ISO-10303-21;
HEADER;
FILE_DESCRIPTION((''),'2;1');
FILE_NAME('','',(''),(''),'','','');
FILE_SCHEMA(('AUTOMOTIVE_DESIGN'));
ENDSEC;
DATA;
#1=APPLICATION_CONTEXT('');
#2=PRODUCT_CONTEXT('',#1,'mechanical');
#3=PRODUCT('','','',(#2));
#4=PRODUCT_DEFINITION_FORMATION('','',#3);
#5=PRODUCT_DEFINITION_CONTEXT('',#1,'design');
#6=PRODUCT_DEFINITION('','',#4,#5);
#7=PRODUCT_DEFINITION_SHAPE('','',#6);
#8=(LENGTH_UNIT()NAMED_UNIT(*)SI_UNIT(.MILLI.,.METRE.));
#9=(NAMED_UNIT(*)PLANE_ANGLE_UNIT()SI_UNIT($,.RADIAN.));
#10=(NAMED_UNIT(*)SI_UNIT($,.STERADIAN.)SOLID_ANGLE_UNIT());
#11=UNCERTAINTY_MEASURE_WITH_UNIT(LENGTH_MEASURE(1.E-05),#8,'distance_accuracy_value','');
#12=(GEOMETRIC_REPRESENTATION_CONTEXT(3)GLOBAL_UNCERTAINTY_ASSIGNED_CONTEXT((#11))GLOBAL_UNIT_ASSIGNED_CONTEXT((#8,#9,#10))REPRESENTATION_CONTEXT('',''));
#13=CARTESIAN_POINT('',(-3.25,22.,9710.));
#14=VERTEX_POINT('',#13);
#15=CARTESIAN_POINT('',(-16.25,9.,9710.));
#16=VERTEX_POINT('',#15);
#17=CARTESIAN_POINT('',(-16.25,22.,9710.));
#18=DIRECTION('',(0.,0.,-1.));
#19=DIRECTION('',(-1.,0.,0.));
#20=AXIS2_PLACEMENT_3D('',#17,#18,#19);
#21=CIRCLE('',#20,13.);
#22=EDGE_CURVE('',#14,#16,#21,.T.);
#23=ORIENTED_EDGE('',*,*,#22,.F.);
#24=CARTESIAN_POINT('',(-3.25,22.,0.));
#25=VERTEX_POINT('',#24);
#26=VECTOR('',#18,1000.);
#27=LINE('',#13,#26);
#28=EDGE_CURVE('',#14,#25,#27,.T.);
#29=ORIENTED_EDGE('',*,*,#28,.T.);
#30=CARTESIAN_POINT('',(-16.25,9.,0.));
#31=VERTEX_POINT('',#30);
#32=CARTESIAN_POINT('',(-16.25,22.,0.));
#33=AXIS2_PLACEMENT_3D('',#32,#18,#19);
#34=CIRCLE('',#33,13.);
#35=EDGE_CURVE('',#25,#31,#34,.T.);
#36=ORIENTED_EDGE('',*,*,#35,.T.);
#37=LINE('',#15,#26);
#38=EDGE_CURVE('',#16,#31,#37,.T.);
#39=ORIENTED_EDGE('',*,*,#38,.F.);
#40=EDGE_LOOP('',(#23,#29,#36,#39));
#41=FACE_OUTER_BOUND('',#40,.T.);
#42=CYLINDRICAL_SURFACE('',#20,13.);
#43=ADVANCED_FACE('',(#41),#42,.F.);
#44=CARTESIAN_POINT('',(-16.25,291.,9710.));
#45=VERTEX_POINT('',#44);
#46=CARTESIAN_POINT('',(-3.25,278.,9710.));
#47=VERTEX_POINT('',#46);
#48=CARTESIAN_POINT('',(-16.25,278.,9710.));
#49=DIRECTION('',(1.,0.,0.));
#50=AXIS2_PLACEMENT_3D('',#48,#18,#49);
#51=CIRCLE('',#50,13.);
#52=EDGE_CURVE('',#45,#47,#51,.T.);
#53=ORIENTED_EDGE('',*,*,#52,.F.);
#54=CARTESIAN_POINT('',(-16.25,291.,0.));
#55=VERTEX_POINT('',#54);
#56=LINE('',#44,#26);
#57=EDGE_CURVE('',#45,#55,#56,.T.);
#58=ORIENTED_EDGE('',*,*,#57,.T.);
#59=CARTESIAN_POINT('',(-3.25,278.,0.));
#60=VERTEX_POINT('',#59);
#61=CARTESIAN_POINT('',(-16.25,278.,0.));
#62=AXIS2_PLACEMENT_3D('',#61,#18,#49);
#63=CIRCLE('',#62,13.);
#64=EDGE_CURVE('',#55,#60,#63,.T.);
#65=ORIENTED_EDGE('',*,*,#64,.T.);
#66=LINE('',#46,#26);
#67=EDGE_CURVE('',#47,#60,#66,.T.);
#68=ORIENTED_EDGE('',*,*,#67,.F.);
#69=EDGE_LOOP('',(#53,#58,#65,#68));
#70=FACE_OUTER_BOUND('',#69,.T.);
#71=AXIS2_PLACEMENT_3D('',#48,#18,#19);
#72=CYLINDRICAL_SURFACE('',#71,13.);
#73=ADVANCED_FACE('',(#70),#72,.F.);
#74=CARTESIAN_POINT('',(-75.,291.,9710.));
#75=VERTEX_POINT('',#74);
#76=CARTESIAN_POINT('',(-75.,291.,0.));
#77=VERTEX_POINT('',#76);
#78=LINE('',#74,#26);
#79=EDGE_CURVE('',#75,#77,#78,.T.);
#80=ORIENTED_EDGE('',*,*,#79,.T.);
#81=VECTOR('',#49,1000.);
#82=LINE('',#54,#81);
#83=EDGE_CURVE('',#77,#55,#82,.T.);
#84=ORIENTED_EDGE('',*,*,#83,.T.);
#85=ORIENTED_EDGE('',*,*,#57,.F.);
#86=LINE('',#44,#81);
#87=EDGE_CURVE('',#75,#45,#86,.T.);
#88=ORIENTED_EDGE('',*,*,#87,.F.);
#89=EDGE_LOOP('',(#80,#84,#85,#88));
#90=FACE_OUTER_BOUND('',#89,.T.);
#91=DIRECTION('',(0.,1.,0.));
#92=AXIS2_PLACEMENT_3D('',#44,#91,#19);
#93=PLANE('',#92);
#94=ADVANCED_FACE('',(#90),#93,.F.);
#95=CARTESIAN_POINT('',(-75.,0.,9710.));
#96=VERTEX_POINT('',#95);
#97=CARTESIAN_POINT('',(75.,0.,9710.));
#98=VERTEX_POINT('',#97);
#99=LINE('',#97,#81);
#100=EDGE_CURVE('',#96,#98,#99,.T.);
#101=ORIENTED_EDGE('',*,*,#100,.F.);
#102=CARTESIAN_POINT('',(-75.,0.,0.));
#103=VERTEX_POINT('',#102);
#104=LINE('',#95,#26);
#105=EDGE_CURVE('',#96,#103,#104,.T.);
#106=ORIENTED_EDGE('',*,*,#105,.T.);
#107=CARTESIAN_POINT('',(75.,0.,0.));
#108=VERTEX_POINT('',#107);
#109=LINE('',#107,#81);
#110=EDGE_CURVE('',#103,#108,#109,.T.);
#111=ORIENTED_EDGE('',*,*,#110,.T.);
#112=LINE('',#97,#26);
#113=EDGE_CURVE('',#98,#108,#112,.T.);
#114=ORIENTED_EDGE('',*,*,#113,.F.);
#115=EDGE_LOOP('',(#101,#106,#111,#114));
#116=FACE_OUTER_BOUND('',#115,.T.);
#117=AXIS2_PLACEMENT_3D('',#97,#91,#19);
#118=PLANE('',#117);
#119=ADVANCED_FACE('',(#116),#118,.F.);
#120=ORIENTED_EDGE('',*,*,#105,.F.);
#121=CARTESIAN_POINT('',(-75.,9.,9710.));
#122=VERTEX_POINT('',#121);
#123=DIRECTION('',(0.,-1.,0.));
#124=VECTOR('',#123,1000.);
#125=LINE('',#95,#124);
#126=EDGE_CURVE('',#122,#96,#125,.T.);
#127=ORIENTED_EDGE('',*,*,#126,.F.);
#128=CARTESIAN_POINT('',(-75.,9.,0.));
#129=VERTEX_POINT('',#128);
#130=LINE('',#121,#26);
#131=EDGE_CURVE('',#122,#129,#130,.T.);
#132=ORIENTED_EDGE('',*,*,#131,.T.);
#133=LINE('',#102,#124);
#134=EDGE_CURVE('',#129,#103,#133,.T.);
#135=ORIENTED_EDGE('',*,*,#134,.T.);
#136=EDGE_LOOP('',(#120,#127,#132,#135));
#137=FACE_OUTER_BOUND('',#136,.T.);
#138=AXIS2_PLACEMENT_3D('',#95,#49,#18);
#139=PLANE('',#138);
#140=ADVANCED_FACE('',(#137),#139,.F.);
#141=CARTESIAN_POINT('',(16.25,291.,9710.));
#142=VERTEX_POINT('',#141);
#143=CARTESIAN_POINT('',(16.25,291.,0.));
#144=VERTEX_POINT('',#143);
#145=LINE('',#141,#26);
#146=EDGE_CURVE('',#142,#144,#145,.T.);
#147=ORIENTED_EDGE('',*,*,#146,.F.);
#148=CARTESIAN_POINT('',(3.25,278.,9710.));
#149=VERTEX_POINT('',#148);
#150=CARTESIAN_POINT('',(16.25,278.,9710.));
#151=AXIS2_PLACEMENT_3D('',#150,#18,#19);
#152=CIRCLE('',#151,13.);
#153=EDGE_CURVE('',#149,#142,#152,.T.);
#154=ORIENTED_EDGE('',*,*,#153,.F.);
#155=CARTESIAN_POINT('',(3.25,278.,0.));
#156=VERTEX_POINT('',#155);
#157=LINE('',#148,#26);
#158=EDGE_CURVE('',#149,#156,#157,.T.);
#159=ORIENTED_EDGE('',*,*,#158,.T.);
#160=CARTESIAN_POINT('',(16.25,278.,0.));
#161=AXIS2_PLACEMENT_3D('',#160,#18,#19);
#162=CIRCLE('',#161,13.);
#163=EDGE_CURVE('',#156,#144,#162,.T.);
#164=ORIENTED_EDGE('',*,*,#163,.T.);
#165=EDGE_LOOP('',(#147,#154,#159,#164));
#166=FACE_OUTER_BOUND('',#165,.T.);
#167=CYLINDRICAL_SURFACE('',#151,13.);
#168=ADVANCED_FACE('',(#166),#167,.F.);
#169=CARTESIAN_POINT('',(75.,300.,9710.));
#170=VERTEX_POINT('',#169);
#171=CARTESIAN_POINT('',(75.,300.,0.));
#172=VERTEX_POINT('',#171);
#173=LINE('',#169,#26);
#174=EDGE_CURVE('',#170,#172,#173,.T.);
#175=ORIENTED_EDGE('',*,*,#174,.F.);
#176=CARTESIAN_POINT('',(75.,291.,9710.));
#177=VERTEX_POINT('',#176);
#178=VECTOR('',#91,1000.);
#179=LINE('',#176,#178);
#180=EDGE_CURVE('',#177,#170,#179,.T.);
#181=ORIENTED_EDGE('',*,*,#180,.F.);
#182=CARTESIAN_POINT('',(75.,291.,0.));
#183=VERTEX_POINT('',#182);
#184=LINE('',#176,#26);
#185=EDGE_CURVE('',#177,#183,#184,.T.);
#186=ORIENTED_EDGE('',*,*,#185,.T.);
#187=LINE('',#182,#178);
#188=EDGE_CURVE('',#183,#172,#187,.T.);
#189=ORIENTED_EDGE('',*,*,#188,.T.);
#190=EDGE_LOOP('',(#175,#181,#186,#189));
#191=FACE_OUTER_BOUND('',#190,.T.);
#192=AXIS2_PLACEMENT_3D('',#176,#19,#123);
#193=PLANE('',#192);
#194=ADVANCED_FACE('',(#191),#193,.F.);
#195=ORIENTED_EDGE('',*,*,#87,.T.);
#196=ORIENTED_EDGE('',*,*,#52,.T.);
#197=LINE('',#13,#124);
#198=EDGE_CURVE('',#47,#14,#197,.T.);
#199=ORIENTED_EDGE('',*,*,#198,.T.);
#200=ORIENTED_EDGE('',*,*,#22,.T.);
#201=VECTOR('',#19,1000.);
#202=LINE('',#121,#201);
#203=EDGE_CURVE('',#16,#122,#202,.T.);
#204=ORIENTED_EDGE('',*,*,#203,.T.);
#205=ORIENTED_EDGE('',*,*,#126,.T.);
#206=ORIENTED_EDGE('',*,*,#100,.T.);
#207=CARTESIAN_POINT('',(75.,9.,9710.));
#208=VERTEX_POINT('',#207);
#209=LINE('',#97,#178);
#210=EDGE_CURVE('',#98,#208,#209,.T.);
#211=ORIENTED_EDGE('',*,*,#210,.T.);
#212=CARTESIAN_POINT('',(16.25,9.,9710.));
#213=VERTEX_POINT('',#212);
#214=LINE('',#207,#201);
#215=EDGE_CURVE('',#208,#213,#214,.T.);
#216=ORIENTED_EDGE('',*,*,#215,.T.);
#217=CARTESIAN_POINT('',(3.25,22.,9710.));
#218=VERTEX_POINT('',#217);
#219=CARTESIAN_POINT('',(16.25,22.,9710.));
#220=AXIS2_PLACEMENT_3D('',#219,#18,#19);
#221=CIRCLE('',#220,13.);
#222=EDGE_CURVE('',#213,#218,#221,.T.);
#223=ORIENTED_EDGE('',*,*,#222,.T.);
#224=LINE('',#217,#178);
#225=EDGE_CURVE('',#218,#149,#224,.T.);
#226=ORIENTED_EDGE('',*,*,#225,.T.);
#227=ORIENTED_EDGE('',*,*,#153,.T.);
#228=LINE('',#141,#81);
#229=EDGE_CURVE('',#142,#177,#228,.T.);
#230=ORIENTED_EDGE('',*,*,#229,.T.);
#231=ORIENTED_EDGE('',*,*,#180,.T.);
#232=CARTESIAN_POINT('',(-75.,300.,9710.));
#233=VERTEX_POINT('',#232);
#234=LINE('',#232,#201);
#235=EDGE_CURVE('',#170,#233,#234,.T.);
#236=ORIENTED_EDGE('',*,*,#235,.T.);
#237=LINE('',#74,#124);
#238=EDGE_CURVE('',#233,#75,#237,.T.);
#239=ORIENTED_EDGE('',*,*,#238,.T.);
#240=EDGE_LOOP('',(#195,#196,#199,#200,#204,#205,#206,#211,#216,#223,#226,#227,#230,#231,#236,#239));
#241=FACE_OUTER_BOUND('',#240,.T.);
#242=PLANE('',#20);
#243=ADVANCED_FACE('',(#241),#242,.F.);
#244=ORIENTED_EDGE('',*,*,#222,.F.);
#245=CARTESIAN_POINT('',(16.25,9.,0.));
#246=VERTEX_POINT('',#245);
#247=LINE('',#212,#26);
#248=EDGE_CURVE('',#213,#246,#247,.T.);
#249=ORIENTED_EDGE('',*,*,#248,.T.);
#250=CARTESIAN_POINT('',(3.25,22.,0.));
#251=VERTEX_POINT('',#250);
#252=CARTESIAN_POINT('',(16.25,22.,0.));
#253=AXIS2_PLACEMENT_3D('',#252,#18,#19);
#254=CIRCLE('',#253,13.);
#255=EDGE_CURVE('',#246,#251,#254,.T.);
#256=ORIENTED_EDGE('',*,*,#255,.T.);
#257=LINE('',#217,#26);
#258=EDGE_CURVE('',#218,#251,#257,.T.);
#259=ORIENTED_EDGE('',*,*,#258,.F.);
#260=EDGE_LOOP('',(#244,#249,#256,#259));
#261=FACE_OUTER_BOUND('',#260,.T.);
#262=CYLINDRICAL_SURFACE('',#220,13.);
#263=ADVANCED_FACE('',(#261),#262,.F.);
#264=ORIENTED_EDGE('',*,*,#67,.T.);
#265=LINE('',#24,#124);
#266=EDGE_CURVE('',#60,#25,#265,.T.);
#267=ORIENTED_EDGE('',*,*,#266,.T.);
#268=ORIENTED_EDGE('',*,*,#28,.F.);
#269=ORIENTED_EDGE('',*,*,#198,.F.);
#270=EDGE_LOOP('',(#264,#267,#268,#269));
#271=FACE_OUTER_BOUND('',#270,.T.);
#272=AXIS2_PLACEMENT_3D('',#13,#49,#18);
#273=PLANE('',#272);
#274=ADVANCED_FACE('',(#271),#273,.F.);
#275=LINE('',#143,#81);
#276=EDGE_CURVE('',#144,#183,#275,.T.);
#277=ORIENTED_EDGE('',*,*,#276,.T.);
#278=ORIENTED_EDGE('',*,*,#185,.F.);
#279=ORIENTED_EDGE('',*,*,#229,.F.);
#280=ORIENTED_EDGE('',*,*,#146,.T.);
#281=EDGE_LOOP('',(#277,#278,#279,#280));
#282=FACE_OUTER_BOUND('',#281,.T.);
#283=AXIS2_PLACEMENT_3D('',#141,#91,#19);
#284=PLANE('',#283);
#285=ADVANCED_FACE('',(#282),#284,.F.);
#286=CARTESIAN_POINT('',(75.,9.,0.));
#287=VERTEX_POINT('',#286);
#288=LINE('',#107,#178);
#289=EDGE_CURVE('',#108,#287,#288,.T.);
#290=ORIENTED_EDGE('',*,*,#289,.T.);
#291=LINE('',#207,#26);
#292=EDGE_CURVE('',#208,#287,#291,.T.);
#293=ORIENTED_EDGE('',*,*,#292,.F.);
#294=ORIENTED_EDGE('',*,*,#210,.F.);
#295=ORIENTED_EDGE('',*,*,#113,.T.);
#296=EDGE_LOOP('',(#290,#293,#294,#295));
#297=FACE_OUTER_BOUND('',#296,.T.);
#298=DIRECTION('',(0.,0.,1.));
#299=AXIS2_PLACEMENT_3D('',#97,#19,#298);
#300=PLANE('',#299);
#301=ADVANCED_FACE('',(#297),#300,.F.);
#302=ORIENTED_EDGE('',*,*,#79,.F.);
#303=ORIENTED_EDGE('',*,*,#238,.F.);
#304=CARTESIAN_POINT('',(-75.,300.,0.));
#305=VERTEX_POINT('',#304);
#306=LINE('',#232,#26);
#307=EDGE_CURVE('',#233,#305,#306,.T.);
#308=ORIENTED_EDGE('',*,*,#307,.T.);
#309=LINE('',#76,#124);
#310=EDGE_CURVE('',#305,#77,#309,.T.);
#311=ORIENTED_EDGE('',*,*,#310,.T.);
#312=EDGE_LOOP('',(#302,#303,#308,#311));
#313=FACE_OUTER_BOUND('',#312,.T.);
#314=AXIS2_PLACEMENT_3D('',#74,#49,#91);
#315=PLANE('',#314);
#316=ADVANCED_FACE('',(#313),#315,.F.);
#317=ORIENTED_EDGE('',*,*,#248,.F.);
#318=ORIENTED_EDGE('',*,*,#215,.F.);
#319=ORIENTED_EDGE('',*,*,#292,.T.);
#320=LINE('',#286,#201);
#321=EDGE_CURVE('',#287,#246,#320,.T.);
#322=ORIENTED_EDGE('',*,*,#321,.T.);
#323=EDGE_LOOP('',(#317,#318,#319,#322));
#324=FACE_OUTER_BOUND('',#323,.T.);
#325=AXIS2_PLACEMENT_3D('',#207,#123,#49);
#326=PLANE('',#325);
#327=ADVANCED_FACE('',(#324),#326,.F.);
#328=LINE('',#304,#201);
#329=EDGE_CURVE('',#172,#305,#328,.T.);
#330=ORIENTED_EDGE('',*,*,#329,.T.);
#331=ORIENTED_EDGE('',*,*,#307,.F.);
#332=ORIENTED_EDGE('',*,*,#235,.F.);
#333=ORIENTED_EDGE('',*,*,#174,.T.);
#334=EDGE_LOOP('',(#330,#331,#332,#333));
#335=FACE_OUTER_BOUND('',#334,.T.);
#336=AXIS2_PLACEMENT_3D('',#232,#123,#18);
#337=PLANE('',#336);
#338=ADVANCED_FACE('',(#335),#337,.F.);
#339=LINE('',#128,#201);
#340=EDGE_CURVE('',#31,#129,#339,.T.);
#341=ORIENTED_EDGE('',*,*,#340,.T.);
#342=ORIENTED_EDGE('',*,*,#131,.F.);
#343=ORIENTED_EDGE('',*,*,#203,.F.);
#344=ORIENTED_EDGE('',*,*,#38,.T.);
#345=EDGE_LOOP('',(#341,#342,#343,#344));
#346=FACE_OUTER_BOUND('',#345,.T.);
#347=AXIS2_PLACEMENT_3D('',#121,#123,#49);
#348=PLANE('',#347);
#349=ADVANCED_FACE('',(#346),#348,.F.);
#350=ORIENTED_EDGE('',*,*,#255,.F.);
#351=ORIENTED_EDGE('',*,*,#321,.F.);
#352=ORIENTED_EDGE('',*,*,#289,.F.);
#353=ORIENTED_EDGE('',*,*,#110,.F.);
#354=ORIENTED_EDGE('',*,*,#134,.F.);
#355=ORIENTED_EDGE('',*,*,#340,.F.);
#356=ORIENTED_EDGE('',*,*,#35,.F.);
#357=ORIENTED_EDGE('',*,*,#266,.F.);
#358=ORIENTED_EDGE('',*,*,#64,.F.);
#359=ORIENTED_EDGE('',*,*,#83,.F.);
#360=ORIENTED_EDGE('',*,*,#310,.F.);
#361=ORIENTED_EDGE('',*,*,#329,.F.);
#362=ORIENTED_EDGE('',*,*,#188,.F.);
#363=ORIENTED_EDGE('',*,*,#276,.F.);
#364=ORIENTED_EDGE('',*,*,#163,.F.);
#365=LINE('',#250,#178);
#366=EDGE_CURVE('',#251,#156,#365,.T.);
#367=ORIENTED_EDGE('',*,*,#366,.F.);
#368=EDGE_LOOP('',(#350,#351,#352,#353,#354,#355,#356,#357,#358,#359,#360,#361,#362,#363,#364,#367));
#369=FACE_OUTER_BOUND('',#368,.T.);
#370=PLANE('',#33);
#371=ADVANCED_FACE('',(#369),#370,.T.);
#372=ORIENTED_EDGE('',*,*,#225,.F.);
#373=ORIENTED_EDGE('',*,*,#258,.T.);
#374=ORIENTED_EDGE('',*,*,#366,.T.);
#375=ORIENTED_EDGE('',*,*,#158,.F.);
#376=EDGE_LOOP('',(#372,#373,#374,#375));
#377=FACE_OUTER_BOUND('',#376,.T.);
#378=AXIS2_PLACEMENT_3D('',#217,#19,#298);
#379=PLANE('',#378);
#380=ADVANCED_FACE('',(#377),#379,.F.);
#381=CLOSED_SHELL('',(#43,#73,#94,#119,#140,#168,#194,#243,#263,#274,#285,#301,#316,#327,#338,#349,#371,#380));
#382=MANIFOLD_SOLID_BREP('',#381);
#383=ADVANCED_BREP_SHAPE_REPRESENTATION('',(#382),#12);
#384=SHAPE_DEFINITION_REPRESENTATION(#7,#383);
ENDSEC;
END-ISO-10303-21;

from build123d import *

# Parameters (mm, degrees)
BOSS_EXTRUDE1_DEPTH = 9710


with BuildPart() as part:
    # Sketch1 → Boss-Extrude1 (new body)
    with BuildSketch(Plane.XY):
        with BuildLine():
            Line((75, 0), (-75, 0))
            Line((-75, 0), (-75, 9))
            Line((-75, 9), (-16.25, 9))
            ThreePointArc((-16.25, 9), (-7.057611845, 12.807611845), (-3.25, 22))
            Line((-3.25, 22), (-3.25, 278))
            ThreePointArc((-3.25, 278), (-7.057611845, 287.192388155), (-16.25, 291))
            Line((-16.25, 291), (-75, 291))
            Line((-75, 291), (-75, 300))
            Line((-75, 300), (75, 300))
            Line((75, 300), (75, 291))
            Line((75, 291), (16.25, 291))
            ThreePointArc((16.25, 291), (7.057611845, 287.192388155), (3.25, 278))
            Line((3.25, 278), (3.25, 22))
            ThreePointArc((3.25, 22), (7.057611845, 12.807611845), (16.25, 9))
            Line((16.25, 9), (75, 9))
            Line((75, 9), (75, 0))
        make_face()
    extrude(amount=BOSS_EXTRUDE1_DEPTH)


solid = part.part
